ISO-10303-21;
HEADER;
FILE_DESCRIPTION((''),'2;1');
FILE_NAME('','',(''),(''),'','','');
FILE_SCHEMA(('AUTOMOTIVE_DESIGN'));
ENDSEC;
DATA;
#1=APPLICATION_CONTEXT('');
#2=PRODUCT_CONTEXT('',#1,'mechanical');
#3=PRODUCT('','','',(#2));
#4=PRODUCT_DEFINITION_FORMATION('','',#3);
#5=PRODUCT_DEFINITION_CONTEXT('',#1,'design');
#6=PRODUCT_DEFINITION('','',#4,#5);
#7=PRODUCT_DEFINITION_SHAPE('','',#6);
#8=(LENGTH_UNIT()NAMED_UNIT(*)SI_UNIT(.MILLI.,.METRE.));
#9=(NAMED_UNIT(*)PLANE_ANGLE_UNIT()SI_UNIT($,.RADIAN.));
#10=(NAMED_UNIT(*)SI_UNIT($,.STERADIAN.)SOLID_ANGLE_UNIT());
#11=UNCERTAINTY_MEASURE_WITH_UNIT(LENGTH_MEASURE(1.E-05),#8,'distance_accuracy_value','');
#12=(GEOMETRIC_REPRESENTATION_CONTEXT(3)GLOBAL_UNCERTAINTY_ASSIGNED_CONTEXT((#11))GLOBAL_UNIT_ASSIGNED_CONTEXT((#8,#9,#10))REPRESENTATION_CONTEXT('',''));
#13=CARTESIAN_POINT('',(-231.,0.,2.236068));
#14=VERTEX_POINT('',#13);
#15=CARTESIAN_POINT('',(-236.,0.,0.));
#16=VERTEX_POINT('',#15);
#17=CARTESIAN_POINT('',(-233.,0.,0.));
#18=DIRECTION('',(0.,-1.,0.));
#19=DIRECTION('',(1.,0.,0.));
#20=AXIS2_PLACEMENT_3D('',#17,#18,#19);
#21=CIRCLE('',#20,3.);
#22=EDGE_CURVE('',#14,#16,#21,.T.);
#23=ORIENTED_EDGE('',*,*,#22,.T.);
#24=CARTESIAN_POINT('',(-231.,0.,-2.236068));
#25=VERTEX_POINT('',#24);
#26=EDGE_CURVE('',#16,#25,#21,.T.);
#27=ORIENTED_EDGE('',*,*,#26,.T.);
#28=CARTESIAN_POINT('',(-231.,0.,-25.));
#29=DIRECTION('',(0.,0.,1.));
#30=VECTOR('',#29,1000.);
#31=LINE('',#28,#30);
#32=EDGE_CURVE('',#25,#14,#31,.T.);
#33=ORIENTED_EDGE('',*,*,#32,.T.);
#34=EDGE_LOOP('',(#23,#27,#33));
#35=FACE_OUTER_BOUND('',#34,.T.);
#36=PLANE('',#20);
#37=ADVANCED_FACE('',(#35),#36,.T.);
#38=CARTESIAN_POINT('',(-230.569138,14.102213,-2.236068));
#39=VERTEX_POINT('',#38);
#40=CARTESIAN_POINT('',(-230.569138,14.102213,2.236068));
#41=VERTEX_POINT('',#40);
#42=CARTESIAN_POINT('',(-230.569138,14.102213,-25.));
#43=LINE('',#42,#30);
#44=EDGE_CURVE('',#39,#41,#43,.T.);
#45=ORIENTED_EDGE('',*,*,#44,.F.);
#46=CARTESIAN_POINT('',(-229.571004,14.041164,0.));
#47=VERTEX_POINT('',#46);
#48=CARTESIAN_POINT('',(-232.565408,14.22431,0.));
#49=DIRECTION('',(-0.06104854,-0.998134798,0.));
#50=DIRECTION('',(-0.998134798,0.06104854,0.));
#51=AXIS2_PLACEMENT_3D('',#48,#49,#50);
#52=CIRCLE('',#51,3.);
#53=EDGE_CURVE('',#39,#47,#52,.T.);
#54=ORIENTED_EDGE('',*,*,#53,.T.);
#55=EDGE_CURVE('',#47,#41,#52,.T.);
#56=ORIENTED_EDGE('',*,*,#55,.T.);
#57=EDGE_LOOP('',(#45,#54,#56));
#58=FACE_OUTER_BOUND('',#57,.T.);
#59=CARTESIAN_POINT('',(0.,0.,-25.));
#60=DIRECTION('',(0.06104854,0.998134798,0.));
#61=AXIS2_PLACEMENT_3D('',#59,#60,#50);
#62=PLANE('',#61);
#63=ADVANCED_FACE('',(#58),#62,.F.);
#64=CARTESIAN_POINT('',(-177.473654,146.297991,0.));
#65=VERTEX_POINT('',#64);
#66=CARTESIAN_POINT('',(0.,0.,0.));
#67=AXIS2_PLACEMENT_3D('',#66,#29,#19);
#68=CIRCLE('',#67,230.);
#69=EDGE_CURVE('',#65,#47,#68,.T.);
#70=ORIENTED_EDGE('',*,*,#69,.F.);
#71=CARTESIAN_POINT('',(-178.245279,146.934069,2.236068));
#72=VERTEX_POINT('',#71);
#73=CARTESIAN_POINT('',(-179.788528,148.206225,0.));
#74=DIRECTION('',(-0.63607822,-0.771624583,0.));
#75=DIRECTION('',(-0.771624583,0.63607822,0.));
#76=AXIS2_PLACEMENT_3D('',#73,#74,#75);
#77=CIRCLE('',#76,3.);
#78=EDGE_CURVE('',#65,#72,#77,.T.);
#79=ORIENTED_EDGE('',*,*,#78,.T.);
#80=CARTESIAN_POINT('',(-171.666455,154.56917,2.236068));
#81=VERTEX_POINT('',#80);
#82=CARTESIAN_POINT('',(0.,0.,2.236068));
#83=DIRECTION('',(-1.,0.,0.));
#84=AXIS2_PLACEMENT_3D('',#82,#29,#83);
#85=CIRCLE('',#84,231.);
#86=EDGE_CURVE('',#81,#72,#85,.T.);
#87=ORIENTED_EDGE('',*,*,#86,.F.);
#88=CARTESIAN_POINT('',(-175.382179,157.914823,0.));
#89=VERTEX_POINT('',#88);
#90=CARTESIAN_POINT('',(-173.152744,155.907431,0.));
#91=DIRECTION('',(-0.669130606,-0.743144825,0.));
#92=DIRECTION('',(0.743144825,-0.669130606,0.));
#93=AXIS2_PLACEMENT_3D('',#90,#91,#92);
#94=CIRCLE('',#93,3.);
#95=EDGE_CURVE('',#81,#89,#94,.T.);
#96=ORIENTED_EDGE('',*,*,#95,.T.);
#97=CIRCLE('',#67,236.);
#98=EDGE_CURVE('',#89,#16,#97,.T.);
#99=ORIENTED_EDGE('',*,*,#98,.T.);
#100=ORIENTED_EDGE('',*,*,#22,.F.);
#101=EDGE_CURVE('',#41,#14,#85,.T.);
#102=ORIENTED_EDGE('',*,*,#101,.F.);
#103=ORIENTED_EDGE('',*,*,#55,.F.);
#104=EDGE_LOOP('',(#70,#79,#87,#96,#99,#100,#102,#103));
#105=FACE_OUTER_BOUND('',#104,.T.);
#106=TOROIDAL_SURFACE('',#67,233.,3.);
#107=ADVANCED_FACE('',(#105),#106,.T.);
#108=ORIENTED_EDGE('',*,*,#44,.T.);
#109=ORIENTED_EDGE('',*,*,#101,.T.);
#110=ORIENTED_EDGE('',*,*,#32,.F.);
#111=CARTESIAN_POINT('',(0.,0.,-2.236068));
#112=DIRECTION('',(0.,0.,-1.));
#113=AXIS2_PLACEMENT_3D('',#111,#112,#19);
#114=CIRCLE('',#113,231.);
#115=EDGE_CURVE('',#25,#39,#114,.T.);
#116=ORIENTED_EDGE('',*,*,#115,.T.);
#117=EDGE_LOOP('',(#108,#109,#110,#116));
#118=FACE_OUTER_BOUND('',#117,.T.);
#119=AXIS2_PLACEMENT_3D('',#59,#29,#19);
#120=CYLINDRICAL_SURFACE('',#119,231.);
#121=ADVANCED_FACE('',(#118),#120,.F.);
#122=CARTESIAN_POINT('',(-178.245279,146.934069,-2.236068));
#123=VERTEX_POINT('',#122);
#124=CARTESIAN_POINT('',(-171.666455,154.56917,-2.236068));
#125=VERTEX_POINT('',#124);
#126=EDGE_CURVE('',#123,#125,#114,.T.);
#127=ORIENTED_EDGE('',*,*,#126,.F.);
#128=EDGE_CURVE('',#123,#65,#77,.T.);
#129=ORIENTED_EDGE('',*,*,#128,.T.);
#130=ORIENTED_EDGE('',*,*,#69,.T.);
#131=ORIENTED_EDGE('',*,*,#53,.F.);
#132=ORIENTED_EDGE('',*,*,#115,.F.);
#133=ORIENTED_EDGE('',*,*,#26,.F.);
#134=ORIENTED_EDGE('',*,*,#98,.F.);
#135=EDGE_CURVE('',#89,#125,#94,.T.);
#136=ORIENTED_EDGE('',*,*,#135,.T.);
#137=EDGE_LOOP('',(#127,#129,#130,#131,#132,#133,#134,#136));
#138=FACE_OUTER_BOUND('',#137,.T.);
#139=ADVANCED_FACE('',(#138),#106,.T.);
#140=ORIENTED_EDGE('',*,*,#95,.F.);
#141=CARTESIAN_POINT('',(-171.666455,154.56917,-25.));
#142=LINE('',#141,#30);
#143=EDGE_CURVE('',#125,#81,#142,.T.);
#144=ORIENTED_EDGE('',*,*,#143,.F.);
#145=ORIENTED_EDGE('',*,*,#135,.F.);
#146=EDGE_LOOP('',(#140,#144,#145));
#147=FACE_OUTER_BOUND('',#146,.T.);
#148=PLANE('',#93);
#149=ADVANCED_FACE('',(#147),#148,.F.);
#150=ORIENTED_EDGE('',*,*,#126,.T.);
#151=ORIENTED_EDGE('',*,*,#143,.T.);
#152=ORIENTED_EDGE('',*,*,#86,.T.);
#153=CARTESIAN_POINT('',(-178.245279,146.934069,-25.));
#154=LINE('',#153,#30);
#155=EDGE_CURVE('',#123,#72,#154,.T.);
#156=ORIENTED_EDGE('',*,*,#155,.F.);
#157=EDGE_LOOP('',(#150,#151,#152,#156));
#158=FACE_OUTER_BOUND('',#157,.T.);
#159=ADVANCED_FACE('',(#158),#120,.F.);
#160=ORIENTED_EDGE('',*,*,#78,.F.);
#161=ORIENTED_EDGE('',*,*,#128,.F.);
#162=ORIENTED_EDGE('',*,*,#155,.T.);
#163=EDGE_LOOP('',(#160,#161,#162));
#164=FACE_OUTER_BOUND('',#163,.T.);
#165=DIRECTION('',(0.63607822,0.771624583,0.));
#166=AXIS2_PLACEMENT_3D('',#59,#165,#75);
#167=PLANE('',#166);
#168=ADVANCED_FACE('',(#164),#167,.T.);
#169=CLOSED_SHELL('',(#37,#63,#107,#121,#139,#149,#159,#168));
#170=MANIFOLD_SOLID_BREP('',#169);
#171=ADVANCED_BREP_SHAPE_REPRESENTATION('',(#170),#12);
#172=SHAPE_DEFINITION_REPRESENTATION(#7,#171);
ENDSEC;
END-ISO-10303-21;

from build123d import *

# Parameters (mm, degrees)
SWEEP1_PROFILE_R   = 3
CUT_EXTRUDE1_DEPTH = 25


with BuildPart() as part:
    # Sweep1: sweep along a path in Sketch1
    with BuildLine(Plane.XY) as sweep1_path:
        ThreePointArc((-173.152744336, 155.907431282), (-217.524239374, 83.499732244), (-233, 0))
    # Sweep1 profile (on start of the path) → Sweep1 (sweep)
    with BuildSketch(Plane(origin=(-173.152744336, 155.907431282, 0), x_dir=(-0.7431448254773938, 0.6691306063588589, 0), z_dir=(-0.6691306063588589, -0.7431448254773938, 0))):
        Circle(SWEEP1_PROFILE_R)
    sweep(path=sweep1_path.line)

    # Sketch6 → Cut-Extrude1 (cut, symmetric)
    with BuildSketch(Plane.XY):
        with BuildLine():
            Line((0, 0), (-230.569138435, 14.102212633))
            ThreePointArc((-230.569138435, 14.102212633), (-230.892259483, 7.054396551), (-231, 0))
            Line((-231, 0), (0, 0))
        make_face()
        with BuildLine():
            Line((0, 0), (-171.666454685, 154.569170069))
            ThreePointArc((-171.666454685, 154.569170069), (-174.997511393, 150.787502819), (-178.245278763, 146.934068884))
            Line((-178.245278763, 146.934068884), (0, 0))
        make_face()
    extrude(amount=CUT_EXTRUDE1_DEPTH, both=True, mode=Mode.SUBTRACT)


solid = part.part
